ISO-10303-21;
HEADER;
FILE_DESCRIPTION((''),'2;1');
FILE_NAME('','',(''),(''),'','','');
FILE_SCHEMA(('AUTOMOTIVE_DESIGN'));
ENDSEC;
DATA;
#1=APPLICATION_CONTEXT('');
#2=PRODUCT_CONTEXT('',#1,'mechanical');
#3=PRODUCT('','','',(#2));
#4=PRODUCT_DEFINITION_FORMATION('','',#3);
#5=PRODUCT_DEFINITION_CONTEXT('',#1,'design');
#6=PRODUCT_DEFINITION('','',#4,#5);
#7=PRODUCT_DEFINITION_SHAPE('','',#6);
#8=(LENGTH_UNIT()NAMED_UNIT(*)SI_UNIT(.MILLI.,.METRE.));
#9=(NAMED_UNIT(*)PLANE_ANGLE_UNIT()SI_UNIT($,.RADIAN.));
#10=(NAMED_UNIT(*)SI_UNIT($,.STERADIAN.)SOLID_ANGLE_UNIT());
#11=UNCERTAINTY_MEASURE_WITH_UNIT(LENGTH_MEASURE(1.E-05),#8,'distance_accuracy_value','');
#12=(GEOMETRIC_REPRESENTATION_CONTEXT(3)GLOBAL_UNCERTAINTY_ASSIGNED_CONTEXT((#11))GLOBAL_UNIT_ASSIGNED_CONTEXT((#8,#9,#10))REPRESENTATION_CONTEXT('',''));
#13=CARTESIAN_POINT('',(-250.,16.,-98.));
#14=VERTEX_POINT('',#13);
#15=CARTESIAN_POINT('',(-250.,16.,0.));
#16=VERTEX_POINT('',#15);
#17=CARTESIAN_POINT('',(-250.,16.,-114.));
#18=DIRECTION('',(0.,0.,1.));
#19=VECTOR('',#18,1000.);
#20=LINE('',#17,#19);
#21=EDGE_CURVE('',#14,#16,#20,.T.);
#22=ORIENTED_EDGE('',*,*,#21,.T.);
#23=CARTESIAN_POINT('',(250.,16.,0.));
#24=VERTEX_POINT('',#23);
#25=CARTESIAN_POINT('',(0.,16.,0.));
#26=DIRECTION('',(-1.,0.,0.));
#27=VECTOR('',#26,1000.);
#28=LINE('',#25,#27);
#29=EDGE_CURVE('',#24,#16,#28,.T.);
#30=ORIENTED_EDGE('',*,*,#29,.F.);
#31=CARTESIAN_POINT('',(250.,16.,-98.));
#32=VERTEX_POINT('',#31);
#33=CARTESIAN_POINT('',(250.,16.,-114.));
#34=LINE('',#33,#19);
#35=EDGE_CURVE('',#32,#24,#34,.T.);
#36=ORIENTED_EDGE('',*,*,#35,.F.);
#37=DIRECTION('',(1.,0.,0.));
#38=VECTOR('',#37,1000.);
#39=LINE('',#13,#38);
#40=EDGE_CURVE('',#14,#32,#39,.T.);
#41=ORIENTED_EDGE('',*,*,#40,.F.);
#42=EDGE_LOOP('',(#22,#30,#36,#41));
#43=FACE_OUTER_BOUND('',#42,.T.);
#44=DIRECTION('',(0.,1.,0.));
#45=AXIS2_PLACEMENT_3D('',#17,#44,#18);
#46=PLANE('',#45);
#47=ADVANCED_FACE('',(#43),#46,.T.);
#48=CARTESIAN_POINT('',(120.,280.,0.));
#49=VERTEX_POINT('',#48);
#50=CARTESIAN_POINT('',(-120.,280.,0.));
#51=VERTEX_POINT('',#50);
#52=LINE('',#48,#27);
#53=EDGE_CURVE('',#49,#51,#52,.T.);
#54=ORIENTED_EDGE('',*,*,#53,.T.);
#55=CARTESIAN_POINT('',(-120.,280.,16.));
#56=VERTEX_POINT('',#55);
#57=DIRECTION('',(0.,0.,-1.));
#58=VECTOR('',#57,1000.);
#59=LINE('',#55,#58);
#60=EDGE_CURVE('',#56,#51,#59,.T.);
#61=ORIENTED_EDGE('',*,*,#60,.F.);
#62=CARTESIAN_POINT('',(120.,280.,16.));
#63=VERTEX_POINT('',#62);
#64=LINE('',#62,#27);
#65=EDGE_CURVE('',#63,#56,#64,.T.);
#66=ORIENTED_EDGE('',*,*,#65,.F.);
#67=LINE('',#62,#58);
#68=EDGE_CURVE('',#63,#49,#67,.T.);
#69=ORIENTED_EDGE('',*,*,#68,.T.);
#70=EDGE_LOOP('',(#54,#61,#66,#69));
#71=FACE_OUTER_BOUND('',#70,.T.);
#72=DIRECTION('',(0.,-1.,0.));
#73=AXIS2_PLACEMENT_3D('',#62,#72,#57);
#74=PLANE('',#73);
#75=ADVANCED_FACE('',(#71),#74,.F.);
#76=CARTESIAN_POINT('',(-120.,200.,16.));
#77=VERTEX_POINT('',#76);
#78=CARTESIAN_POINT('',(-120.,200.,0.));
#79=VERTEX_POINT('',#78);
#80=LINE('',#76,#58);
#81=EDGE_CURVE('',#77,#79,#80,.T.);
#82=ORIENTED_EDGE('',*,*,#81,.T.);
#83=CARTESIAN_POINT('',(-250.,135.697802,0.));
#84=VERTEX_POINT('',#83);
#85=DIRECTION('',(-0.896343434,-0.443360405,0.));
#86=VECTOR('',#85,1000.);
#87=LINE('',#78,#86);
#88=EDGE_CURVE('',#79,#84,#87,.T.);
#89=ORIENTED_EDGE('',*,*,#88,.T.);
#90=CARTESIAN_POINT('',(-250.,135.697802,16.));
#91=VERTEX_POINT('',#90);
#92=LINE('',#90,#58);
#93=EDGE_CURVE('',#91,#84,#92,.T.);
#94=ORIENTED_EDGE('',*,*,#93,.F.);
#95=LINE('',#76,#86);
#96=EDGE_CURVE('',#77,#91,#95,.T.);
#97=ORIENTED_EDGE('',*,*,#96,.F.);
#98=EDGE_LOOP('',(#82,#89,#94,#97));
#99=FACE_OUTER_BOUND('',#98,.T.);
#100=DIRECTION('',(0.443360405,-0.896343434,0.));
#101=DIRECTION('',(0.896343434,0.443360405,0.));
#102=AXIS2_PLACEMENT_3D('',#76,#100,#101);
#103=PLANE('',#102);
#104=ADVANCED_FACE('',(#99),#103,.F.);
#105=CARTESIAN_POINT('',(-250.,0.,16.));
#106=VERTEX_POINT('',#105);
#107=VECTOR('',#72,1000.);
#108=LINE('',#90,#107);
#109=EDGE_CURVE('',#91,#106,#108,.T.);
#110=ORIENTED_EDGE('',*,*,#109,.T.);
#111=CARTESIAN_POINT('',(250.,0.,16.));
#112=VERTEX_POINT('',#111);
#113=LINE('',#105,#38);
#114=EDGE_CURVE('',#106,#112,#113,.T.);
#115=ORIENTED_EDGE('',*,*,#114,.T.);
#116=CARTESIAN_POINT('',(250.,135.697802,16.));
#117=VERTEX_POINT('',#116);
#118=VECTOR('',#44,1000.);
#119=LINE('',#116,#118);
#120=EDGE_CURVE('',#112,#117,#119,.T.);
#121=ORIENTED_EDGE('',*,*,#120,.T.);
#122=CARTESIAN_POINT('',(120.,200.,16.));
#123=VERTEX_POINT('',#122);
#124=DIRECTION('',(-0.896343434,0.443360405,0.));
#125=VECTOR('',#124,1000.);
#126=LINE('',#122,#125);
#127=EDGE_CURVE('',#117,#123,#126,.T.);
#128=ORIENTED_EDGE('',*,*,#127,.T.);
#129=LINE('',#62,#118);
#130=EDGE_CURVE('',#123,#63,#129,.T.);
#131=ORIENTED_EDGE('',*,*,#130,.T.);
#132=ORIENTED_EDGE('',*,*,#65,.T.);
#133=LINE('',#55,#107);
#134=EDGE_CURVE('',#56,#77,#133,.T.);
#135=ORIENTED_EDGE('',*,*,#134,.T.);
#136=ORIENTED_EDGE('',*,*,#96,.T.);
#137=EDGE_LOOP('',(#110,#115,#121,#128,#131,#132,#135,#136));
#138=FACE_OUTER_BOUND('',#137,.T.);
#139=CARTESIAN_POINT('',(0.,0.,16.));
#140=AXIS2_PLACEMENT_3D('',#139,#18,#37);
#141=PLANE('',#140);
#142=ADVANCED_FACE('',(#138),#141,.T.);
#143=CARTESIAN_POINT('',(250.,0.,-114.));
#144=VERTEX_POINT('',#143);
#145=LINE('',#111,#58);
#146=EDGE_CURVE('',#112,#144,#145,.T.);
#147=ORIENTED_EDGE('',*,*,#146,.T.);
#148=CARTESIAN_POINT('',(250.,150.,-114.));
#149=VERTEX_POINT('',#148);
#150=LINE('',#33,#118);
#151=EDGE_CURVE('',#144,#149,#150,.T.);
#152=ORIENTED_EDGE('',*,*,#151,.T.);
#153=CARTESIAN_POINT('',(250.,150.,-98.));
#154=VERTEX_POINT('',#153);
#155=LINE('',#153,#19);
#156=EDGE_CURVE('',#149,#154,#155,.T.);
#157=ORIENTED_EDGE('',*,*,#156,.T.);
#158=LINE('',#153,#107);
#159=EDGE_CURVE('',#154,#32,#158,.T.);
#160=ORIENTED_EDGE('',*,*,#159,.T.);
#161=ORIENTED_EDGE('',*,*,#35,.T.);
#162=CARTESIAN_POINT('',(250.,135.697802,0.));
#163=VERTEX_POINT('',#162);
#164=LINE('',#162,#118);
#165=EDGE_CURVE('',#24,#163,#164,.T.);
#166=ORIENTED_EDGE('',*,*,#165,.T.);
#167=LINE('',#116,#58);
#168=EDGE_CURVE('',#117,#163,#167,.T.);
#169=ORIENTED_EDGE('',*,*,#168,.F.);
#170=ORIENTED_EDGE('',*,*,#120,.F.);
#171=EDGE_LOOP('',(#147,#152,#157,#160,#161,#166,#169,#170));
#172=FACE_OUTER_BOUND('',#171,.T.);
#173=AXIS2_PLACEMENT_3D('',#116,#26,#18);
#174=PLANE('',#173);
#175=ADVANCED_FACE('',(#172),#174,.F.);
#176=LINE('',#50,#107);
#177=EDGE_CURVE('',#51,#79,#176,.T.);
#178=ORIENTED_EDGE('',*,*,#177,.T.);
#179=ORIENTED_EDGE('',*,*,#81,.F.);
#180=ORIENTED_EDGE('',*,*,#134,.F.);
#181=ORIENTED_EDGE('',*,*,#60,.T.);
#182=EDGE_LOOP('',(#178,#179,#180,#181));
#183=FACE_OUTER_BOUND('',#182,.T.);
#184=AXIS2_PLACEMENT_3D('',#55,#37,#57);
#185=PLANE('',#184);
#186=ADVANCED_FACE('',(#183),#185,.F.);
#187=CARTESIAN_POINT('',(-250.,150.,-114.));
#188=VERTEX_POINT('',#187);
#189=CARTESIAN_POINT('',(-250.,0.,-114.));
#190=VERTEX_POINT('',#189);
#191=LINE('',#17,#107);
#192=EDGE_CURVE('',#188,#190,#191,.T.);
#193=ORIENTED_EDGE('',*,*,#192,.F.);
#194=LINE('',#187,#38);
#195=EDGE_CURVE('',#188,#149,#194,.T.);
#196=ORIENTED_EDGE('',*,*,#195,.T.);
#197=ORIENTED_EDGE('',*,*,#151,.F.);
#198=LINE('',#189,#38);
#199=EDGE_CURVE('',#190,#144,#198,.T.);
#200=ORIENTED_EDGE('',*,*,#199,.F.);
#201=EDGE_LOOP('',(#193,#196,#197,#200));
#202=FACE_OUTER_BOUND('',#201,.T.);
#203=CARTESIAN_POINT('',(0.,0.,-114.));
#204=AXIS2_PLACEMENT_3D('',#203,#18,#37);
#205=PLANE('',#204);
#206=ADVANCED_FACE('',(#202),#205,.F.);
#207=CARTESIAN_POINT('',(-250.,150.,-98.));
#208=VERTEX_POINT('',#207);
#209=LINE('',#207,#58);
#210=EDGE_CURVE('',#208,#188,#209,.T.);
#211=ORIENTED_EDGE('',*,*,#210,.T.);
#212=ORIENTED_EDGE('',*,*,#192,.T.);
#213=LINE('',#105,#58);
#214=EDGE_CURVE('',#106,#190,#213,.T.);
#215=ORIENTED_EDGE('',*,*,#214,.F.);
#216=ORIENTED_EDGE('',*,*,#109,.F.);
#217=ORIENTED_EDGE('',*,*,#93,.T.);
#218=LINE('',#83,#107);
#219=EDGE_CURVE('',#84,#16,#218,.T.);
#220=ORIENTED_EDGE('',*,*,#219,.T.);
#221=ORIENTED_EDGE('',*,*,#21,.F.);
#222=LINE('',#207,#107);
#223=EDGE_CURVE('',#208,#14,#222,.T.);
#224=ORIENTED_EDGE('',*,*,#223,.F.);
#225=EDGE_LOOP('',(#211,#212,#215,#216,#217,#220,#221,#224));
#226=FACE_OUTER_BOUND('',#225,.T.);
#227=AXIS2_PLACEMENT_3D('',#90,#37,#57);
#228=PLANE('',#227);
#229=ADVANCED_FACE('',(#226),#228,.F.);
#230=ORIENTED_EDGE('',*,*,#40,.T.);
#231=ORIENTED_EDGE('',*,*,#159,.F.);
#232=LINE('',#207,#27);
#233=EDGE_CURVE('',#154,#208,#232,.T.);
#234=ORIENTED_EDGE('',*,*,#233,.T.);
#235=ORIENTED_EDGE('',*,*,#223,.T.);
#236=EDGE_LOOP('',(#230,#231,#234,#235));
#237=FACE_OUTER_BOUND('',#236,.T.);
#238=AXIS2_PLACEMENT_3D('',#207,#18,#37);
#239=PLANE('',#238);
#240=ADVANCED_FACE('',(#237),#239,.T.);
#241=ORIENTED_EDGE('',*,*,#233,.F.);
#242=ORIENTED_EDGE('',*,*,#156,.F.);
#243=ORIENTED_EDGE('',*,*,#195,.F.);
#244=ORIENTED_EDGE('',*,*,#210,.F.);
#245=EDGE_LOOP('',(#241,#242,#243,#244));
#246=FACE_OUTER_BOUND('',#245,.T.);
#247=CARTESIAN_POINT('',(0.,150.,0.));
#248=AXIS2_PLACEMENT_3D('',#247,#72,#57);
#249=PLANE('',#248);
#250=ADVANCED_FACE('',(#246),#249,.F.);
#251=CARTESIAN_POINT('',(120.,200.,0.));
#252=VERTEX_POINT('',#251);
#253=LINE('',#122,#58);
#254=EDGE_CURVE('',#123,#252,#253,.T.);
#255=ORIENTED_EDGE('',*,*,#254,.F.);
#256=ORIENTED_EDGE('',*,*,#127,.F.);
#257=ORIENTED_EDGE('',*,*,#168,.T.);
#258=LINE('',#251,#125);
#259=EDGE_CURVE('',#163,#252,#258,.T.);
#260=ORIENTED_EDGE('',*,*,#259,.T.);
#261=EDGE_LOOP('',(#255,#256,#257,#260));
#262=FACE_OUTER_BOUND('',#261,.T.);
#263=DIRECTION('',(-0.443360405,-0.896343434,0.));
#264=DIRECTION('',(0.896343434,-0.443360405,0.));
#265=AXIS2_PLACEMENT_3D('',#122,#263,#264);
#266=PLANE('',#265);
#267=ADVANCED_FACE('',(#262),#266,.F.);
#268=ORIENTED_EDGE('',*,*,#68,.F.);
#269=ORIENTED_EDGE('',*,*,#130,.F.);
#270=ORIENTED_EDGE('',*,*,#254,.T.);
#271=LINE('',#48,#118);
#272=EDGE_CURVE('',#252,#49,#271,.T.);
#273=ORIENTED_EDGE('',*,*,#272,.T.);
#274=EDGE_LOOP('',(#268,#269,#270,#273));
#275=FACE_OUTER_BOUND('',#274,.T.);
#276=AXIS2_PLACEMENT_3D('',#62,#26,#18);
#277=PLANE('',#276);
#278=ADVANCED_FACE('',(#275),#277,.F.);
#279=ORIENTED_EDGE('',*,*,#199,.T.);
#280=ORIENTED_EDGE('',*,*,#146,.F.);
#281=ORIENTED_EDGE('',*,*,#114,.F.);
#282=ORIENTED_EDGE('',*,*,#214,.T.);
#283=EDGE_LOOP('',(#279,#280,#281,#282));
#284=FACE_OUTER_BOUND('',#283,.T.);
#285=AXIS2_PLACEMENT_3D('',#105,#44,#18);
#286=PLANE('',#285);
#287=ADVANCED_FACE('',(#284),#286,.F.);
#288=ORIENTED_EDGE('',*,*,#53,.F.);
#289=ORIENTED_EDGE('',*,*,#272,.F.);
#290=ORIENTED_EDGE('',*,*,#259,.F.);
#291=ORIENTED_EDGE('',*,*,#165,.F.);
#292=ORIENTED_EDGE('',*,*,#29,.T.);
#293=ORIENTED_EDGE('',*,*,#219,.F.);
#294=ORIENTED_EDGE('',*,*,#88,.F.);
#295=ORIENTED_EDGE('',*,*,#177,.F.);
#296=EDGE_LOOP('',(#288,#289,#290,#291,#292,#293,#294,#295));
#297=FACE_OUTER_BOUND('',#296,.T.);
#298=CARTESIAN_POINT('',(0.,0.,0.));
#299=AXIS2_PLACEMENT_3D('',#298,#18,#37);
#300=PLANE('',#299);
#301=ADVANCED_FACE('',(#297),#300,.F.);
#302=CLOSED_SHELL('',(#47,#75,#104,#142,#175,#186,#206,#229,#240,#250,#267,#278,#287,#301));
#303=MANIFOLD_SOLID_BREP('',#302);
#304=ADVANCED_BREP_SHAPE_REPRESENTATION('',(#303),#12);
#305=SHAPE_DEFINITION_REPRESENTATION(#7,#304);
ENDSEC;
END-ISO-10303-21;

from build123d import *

# Parameters (mm, degrees)
BOSS_EXTRUDE1_DEPTH = 16
SKETCH2_W           = 500
SKETCH2_H           = 16
BOSS_EXTRUDE2_DEPTH = 130
SKETCH3_W           = 500
SKETCH3_H           = 16
BOSS_EXTRUDE3_DEPTH = 150


with BuildPart() as part:
    # Sketch1 → Boss-Extrude1 (new body)
    with BuildSketch(Plane.XY):
        Polygon((120, 280), (-120, 280), (-120, 200), (-250, 135.697802275), (-250, 0), (250, 0), (250, 135.697802275), (120, 200), align=None)
    extrude(amount=BOSS_EXTRUDE1_DEPTH)

    # Sketch2 → Boss-Extrude2 (add)
    with BuildSketch(Plane.XY.offset(16)):
        with Locations((0, 8)):
            Rectangle(SKETCH2_W, SKETCH2_H)
    extrude(amount=-BOSS_EXTRUDE2_DEPTH)

    # Sketch3 → Boss-Extrude3 (add)
    with BuildSketch(Plane(origin=(0, 0, 0), x_dir=(-1, 0, 0), z_dir=(0, -1, 0))):
        with Locations((0, 106)):
            Rectangle(SKETCH3_W, SKETCH3_H)
    extrude(amount=-BOSS_EXTRUDE3_DEPTH)


solid = part.part
